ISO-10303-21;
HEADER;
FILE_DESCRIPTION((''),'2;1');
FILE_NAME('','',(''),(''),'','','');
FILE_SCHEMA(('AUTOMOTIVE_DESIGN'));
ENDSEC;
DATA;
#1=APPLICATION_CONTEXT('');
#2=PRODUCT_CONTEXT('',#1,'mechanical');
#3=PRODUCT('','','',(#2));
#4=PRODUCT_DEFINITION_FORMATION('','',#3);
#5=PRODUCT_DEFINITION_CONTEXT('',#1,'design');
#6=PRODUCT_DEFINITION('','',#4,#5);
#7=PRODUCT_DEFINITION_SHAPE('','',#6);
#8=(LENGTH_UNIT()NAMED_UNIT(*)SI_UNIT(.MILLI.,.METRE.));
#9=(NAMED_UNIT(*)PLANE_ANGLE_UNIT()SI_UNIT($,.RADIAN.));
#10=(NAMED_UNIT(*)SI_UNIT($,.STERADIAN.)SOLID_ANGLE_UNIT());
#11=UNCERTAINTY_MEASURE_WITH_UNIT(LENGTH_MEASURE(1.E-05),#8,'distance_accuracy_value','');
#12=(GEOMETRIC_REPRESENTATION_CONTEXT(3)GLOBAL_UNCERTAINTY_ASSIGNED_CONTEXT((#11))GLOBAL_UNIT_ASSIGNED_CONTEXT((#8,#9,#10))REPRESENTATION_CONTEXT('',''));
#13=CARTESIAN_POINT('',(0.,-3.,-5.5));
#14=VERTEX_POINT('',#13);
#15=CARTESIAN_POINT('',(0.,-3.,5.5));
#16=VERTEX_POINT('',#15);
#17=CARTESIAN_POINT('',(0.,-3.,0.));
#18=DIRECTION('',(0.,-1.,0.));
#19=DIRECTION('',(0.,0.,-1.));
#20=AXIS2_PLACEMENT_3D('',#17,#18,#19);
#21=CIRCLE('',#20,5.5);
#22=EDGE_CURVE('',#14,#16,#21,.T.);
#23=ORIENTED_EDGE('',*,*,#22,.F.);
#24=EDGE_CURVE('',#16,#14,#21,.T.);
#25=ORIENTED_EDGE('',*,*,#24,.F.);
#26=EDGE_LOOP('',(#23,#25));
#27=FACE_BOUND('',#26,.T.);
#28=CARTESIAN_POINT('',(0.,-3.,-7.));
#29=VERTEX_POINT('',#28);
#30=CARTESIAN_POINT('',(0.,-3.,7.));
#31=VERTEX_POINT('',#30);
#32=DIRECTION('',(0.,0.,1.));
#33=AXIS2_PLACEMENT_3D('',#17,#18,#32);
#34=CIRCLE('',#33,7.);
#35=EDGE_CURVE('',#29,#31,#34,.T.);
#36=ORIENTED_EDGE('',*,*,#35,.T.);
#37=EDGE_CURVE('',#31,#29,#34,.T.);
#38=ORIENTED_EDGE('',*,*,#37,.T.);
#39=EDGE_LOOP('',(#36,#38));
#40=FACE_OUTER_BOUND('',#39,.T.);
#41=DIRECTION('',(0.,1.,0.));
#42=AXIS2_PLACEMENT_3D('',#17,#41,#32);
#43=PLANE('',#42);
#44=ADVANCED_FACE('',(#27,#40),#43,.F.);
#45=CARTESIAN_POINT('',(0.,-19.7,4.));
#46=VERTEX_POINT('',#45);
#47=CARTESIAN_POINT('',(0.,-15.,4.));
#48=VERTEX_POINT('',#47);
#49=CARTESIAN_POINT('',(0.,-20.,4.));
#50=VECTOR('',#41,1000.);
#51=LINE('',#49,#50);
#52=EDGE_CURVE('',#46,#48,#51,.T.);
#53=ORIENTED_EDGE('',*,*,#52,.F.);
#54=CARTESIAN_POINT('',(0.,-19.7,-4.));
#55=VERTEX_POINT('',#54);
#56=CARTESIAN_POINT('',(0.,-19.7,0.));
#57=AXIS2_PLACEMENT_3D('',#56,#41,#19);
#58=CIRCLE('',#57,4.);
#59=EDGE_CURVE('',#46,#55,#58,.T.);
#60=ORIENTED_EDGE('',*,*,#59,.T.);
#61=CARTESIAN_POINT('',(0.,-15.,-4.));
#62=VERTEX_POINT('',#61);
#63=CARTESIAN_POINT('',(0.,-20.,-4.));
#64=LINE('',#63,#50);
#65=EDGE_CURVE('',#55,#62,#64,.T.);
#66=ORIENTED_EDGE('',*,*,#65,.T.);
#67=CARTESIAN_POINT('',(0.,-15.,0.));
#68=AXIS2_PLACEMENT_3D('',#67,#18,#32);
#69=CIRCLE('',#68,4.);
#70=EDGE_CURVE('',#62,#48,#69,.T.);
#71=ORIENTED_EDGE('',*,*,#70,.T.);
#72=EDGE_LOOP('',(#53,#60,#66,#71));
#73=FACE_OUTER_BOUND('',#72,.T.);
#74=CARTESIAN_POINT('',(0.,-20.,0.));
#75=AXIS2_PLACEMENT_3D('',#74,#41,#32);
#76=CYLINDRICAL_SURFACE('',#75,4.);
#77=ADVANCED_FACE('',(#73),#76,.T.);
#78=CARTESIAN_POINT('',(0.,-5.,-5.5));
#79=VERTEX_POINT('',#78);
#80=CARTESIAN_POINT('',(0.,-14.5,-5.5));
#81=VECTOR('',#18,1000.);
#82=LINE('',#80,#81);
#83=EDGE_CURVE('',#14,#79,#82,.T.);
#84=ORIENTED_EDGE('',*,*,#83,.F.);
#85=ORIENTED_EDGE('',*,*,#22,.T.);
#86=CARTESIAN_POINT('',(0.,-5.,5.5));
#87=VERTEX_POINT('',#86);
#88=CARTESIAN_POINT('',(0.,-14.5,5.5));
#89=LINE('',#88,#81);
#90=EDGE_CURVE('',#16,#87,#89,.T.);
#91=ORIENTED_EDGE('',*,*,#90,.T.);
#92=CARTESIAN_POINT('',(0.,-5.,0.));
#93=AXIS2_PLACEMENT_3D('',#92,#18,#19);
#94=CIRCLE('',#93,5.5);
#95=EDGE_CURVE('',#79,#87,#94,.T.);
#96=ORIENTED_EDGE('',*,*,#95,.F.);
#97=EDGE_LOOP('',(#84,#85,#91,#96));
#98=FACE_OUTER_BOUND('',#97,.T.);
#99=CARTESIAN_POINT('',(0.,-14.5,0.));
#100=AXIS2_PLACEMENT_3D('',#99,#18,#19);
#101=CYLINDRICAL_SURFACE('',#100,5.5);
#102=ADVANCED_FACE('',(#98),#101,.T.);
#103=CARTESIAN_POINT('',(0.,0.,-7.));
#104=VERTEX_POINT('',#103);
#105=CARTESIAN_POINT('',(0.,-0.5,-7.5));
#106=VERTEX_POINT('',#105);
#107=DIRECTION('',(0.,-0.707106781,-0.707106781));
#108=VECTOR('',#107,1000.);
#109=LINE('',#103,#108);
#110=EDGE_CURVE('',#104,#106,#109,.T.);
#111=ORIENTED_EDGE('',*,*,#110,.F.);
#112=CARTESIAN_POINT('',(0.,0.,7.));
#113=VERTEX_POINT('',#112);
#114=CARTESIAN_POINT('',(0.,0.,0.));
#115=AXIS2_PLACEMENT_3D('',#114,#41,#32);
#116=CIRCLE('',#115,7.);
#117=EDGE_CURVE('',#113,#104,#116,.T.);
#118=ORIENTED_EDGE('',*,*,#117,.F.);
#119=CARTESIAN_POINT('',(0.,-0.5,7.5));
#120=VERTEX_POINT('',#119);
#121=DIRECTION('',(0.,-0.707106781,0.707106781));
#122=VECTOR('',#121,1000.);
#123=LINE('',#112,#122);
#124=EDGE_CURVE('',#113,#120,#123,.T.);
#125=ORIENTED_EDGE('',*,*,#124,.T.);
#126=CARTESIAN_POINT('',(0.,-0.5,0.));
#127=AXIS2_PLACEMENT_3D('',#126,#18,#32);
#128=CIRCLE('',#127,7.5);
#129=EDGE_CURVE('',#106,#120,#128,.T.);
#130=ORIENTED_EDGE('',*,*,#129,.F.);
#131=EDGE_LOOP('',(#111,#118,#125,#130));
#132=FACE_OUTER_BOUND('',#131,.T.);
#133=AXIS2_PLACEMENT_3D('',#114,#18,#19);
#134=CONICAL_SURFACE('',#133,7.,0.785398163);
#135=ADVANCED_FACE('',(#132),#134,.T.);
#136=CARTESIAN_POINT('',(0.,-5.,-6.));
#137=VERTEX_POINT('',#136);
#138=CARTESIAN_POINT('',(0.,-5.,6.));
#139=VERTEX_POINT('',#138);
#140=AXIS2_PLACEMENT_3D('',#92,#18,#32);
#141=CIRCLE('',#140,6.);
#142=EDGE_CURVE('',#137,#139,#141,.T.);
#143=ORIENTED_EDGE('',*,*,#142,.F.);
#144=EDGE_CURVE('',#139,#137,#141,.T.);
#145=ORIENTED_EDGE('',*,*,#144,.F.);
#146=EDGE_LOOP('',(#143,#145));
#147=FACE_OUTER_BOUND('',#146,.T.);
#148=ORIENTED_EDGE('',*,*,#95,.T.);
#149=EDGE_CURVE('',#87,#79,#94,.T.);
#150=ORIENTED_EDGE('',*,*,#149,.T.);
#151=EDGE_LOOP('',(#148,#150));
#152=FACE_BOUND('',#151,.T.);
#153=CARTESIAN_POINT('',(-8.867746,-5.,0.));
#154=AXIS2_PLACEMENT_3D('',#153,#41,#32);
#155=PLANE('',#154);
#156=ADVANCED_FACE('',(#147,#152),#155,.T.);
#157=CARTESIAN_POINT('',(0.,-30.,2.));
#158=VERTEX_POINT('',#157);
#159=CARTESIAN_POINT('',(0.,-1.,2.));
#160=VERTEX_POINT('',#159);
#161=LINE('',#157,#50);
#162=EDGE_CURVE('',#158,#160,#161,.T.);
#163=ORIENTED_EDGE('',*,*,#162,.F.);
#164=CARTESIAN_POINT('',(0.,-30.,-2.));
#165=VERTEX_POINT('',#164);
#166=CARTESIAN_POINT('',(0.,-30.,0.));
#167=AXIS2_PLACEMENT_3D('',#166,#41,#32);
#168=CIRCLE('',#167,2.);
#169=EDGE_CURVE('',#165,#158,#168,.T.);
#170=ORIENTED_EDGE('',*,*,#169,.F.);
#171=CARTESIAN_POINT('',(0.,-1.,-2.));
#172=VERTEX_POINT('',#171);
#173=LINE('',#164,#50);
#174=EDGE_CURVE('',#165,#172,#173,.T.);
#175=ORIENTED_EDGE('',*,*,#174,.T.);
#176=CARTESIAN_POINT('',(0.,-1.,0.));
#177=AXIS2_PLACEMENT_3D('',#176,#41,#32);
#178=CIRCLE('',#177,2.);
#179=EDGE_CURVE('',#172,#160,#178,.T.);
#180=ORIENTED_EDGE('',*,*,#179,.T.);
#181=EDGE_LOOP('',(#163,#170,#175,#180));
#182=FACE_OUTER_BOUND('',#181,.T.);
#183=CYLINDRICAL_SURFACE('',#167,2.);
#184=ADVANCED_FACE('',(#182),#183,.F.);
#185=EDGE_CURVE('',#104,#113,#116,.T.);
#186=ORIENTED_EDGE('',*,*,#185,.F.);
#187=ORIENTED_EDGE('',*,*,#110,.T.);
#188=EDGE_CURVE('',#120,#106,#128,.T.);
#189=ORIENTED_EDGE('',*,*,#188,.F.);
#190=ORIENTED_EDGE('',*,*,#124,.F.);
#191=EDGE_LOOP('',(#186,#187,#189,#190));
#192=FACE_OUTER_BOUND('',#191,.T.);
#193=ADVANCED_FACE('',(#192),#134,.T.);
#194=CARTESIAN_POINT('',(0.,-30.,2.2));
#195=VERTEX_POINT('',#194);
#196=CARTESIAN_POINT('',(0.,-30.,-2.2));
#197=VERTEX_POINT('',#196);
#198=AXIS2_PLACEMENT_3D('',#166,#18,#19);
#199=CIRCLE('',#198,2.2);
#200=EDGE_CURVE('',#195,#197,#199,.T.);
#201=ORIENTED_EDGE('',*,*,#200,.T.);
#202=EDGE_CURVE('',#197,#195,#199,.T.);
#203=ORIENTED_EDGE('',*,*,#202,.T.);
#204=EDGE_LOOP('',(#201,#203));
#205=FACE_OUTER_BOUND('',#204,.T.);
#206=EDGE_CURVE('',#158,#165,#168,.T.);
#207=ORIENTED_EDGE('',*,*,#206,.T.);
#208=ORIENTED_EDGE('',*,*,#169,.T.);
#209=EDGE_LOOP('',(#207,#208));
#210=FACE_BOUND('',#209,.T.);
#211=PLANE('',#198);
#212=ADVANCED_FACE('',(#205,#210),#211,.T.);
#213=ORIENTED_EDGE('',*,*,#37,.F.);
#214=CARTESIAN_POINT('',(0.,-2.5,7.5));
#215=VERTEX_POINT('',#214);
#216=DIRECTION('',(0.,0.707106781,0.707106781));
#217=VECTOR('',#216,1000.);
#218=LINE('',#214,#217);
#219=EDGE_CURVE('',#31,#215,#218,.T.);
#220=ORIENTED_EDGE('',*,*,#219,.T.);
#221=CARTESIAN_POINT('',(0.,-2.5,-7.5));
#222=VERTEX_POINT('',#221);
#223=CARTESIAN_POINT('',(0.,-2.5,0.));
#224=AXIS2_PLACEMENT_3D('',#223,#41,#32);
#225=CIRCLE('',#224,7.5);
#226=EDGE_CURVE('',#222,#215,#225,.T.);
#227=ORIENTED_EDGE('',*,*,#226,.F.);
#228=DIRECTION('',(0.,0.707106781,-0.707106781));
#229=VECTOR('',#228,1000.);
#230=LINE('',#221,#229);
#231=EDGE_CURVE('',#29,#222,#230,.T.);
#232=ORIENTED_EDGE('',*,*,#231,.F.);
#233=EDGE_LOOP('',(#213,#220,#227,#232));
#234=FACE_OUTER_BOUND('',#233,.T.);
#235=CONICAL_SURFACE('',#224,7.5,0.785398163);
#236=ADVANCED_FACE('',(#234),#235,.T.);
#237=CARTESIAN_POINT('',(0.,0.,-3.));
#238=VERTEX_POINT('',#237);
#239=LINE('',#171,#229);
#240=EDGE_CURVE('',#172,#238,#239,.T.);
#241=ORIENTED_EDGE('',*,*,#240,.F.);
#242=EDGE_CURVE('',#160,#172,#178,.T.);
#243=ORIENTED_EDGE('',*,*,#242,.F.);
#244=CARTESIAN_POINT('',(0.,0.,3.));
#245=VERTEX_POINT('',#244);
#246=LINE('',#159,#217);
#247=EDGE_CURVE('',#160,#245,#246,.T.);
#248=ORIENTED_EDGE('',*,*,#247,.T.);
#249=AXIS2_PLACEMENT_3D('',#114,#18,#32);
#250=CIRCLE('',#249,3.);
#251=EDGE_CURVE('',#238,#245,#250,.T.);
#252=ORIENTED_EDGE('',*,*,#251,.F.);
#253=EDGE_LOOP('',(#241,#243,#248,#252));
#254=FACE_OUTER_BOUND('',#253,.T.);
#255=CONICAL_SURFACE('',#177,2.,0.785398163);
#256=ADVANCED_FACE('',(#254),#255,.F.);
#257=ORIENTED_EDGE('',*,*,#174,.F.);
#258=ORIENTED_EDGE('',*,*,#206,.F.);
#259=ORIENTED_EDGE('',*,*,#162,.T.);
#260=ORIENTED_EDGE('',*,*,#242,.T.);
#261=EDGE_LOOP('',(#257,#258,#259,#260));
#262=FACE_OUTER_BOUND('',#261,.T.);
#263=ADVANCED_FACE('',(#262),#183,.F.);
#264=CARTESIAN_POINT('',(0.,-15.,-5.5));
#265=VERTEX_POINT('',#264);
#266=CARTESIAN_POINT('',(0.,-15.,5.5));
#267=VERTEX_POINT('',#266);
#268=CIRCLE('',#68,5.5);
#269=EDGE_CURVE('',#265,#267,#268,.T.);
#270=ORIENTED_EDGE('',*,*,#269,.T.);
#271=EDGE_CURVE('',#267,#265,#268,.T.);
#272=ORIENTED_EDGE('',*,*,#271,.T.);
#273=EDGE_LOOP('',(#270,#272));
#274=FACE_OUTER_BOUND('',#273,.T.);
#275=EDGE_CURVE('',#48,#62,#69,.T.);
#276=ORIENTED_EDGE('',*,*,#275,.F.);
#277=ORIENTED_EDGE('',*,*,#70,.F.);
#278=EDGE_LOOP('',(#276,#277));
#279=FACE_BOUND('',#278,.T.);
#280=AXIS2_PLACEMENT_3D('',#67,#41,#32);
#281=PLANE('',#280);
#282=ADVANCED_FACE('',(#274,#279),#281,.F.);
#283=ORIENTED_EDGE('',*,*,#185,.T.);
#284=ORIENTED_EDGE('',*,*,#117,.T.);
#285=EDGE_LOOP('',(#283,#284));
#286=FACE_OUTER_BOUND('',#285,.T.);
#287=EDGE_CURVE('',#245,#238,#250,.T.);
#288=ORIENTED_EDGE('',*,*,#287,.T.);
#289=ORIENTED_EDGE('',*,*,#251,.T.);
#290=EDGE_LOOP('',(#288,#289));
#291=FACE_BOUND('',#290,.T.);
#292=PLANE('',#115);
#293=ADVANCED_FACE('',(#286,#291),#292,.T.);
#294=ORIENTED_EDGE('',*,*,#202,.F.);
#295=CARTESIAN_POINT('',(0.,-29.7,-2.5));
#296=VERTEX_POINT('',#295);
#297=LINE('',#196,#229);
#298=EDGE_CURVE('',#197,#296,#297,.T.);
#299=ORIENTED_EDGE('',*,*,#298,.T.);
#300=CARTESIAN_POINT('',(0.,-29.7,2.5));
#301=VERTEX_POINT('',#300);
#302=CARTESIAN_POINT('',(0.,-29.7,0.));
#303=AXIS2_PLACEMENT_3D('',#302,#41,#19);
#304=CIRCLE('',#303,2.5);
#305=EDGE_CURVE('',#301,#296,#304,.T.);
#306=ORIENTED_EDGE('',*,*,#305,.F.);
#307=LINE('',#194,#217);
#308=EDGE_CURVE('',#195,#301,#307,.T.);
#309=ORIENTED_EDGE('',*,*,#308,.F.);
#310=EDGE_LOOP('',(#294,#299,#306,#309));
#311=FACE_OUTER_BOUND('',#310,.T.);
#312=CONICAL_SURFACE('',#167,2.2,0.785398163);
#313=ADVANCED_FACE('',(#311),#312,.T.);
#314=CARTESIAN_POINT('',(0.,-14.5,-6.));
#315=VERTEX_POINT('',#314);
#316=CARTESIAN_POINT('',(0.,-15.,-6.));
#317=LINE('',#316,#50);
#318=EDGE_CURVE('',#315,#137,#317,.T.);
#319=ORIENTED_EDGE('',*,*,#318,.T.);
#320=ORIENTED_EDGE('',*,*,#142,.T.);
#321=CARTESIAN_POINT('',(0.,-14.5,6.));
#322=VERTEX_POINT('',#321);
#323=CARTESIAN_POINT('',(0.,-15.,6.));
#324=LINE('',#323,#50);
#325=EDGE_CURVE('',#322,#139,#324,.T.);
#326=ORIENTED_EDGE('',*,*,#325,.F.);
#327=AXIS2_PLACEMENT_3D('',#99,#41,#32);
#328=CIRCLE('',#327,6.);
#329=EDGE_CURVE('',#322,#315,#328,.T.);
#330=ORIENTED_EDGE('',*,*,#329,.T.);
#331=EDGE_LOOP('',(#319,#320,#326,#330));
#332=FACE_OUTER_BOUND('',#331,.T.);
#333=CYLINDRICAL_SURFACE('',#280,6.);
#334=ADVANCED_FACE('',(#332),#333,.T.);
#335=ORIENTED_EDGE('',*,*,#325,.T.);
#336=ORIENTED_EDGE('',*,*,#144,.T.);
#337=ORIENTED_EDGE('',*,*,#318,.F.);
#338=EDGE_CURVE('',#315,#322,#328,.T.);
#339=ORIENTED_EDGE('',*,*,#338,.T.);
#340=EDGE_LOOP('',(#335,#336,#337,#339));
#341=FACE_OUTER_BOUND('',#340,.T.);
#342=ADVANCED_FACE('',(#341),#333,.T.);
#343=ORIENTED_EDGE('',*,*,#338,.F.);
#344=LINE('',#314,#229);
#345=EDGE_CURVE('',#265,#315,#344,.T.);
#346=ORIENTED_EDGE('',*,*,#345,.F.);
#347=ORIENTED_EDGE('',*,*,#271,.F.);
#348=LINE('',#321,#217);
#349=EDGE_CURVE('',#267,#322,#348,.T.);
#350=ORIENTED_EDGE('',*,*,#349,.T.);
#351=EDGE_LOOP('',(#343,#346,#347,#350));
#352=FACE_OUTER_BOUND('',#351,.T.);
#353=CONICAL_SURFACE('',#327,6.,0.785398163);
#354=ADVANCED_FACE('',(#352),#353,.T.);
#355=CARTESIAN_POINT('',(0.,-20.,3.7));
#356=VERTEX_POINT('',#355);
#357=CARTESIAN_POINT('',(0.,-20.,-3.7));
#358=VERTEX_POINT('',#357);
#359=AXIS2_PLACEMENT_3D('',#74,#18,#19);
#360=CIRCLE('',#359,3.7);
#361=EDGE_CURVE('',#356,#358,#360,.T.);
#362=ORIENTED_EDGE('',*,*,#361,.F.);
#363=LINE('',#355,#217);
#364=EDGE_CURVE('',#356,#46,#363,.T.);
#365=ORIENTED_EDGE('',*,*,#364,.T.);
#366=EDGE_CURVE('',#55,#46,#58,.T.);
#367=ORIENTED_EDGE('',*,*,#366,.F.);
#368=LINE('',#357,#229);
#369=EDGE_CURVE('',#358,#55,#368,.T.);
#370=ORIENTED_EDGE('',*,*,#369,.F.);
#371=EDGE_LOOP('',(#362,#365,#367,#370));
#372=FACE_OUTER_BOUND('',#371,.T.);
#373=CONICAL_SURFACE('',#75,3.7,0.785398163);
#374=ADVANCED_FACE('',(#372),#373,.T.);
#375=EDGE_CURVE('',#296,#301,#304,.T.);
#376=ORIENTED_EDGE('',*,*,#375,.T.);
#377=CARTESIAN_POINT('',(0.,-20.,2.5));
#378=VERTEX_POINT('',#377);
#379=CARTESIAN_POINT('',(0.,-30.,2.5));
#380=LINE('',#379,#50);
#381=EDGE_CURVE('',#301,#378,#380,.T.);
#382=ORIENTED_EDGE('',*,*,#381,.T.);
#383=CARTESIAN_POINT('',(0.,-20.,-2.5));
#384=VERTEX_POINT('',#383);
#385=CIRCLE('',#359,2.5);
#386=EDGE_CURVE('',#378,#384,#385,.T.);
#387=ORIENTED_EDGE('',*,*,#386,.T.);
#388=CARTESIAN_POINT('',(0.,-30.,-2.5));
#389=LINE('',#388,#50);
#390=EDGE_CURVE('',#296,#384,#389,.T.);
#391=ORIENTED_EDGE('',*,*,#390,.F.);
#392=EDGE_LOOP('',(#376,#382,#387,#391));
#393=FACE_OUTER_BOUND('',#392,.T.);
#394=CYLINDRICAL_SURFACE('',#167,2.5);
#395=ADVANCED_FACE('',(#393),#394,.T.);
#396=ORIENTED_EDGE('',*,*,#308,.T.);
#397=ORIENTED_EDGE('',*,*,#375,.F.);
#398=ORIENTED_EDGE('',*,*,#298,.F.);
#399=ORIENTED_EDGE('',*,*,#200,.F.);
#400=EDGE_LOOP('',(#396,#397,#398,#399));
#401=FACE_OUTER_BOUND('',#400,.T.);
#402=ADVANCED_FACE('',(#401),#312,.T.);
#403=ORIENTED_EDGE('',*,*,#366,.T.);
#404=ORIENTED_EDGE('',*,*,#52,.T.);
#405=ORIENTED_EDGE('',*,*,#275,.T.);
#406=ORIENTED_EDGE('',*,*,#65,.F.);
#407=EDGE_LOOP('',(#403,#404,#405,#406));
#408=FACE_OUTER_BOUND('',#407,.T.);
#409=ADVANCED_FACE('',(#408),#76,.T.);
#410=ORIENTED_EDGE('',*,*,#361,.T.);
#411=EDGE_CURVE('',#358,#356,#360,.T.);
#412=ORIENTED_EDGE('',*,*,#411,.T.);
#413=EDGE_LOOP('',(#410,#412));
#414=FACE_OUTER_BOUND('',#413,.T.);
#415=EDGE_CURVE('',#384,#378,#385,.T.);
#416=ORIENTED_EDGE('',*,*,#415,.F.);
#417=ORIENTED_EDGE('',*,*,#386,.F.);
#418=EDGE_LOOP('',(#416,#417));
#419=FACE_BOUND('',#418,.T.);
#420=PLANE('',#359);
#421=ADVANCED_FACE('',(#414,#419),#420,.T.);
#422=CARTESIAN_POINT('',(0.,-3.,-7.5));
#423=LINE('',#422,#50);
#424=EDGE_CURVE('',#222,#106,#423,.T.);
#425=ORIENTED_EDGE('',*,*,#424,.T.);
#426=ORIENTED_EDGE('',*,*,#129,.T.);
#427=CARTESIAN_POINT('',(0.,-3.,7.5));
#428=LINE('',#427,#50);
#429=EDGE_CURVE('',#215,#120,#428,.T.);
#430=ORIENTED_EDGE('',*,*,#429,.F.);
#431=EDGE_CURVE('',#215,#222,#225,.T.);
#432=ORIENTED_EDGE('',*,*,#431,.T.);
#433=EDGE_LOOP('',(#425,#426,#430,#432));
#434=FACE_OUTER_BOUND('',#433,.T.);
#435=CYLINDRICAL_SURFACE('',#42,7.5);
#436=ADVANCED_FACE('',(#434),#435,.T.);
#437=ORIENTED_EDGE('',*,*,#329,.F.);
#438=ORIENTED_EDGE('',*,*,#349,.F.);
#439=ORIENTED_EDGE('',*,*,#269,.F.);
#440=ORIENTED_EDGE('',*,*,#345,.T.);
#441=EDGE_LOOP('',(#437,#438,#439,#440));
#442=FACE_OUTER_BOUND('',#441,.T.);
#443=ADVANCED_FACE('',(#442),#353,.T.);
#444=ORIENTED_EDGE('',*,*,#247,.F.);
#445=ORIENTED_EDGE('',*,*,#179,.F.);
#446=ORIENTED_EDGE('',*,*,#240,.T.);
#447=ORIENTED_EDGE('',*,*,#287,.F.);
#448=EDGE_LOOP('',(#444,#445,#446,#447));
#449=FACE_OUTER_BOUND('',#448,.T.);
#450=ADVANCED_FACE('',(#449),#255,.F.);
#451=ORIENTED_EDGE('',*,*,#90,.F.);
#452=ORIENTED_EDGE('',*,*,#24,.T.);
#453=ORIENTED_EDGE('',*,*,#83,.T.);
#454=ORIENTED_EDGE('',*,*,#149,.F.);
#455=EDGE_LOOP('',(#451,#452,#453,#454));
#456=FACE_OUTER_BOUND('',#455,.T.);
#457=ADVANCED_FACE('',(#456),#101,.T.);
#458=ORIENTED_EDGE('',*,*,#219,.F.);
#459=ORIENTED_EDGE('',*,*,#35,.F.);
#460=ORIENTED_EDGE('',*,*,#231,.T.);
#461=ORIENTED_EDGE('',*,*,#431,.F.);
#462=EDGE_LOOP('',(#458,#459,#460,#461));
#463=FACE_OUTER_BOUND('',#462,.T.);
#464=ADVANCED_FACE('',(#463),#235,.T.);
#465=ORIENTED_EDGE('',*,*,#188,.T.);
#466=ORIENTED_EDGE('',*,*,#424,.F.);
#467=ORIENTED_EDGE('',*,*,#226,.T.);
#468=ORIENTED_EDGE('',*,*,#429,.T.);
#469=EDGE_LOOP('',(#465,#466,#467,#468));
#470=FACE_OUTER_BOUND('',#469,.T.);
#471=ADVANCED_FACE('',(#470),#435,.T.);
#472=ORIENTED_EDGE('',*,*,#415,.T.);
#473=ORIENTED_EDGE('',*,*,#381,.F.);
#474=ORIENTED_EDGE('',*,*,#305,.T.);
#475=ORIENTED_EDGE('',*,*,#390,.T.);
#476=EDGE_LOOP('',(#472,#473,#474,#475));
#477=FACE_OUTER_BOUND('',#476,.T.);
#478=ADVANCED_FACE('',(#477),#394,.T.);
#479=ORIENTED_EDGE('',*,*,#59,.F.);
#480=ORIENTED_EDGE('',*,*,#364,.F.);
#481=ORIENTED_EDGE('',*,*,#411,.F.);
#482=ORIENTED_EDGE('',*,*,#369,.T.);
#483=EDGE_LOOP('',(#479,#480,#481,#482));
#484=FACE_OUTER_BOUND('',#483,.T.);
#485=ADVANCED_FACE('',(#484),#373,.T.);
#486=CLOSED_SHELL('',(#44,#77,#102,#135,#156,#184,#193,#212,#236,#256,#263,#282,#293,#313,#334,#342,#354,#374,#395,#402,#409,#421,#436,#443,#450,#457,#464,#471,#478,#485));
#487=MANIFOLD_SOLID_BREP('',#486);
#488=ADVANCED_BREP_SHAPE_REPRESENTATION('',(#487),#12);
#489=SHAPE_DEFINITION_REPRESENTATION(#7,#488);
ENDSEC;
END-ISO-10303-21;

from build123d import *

# Parameters (mm, degrees)
SKETCH_1_R          = 6
EXTRUDE_1_DEPTH     = 15
SKETCH_2_R          = 2.5
EXTRUDE_2_DEPTH     = 15
SKETCH_3_R          = 2
CUT_EXTRUDE_1_DEPTH = 32.176914536
CHAMFER_2_SIZE      = 0.5
SKETCH_6_R          = 7.5
SKETCH_6_R_2        = 6
EXTRUDE_3_DEPTH     = 3
CHAMFER_3_SIZE      = 1
CHAMFER_4_SIZE      = 0.5
SKETCH_7_R          = 4
SKETCH_7_R_2        = 2.5
EXTRUDE_4_DEPTH     = 5
CHAMFER_5_SIZE      = 0.3
CHAMFER_6_SIZE      = 0.3
SKETCH_8_W          = 3.367745964
SKETCH_8_H          = 2


with BuildPart() as part:
    # 草图1 → 凸台-拉伸1 (new body)
    with BuildSketch(Plane(origin=(0, 0, 0), x_dir=(1, 0, 0), z_dir=(0, 1, 0))):
        with Locations(Location((0, 0, 0), (0, 0, 270))):
            Circle(SKETCH_1_R)
    extrude(amount=-EXTRUDE_1_DEPTH)

    # 草图2 → 凸台-拉伸2 (add)
    with BuildSketch(Plane.XZ.offset(15)):
        with Locations(Location((0, 0, 0), (0, 0, 90))):
            Circle(SKETCH_2_R)
    extrude(amount=EXTRUDE_2_DEPTH)

    # 草图3 → 切除-拉伸1 (cut, through all)
    with BuildSketch(Plane(origin=(0, 0, 0), x_dir=(1, 0, 0), z_dir=(0, 1, 0))):
        with Locations(Location((0, 0, 0), (0, 0, 270))):
            Circle(SKETCH_3_R)
    extrude(amount=-CUT_EXTRUDE_1_DEPTH, mode=Mode.SUBTRACT)

    # 倒角2
    chamfer_2_edges = [part.edges().sort_by_distance(p)[0] for p in [
        (0, -15, -6),
    ]]
    chamfer(chamfer_2_edges, length=CHAMFER_2_SIZE)

    # 草图6 → 凸台-拉伸3 (add)
    with BuildSketch(Plane(origin=(0, 0, 0), x_dir=(1, 0, 0), z_dir=(0, 1, 0))):
        with Locations(Location((0, 0, 0), (0, 0, 270))):
            Circle(SKETCH_6_R)
        with Locations(Location((0, 0, 0), (0, 0, 270))):
            Circle(SKETCH_6_R_2, mode=Mode.SUBTRACT)
    extrude(amount=-EXTRUDE_3_DEPTH)

    # 倒角3
    chamfer_3_edges = [part.edges().sort_by_distance(p)[0] for p in [
        (0, 0, -2),
    ]]
    chamfer(chamfer_3_edges, length=CHAMFER_3_SIZE)

    # 倒角4
    chamfer_4_edges = [part.edges().sort_by_distance(p)[0] for p in [
        (0, -3, -7.5),
        (0, 0, -7.5),
    ]]
    chamfer(chamfer_4_edges, length=CHAMFER_4_SIZE)

    # 草图7 → 凸台-拉伸4 (add)
    with BuildSketch(Plane.XZ.offset(15)):
        with Locations(Location((0, 0, 0), (0, 0, 90))):
            Circle(SKETCH_7_R)
        with Locations(Location((0, 0, 0), (0, 0, 270))):
            Circle(SKETCH_7_R_2, mode=Mode.SUBTRACT)
    extrude(amount=EXTRUDE_4_DEPTH)

    # 倒角5
    chamfer_5_edges = [part.edges().sort_by_distance(p)[0] for p in [
        (0, -20, -4),
    ]]
    chamfer(chamfer_5_edges, length=CHAMFER_5_SIZE)

    # 倒角6
    chamfer_6_edges = [part.edges().sort_by_distance(p)[0] for p in [
        (0, -30, -2.5),
    ]]
    chamfer(chamfer_6_edges, length=CHAMFER_6_SIZE)

    # 草图8 → 切除-旋转1 (revolve, cut)
    with BuildSketch(Plane.XY, mode=Mode.PRIVATE) as cut_revolve_1_sk:
        with Locations((-7.183872982, -4)):
            Rectangle(SKETCH_8_W, SKETCH_8_H)
    revolve(cut_revolve_1_sk.sketch.rotate(Axis((0, -15, 0), (0, 1, 0)), 90), axis=Axis((0, -15, 0), (0, 1, 0)), mode=Mode.SUBTRACT)


solid = part.part
